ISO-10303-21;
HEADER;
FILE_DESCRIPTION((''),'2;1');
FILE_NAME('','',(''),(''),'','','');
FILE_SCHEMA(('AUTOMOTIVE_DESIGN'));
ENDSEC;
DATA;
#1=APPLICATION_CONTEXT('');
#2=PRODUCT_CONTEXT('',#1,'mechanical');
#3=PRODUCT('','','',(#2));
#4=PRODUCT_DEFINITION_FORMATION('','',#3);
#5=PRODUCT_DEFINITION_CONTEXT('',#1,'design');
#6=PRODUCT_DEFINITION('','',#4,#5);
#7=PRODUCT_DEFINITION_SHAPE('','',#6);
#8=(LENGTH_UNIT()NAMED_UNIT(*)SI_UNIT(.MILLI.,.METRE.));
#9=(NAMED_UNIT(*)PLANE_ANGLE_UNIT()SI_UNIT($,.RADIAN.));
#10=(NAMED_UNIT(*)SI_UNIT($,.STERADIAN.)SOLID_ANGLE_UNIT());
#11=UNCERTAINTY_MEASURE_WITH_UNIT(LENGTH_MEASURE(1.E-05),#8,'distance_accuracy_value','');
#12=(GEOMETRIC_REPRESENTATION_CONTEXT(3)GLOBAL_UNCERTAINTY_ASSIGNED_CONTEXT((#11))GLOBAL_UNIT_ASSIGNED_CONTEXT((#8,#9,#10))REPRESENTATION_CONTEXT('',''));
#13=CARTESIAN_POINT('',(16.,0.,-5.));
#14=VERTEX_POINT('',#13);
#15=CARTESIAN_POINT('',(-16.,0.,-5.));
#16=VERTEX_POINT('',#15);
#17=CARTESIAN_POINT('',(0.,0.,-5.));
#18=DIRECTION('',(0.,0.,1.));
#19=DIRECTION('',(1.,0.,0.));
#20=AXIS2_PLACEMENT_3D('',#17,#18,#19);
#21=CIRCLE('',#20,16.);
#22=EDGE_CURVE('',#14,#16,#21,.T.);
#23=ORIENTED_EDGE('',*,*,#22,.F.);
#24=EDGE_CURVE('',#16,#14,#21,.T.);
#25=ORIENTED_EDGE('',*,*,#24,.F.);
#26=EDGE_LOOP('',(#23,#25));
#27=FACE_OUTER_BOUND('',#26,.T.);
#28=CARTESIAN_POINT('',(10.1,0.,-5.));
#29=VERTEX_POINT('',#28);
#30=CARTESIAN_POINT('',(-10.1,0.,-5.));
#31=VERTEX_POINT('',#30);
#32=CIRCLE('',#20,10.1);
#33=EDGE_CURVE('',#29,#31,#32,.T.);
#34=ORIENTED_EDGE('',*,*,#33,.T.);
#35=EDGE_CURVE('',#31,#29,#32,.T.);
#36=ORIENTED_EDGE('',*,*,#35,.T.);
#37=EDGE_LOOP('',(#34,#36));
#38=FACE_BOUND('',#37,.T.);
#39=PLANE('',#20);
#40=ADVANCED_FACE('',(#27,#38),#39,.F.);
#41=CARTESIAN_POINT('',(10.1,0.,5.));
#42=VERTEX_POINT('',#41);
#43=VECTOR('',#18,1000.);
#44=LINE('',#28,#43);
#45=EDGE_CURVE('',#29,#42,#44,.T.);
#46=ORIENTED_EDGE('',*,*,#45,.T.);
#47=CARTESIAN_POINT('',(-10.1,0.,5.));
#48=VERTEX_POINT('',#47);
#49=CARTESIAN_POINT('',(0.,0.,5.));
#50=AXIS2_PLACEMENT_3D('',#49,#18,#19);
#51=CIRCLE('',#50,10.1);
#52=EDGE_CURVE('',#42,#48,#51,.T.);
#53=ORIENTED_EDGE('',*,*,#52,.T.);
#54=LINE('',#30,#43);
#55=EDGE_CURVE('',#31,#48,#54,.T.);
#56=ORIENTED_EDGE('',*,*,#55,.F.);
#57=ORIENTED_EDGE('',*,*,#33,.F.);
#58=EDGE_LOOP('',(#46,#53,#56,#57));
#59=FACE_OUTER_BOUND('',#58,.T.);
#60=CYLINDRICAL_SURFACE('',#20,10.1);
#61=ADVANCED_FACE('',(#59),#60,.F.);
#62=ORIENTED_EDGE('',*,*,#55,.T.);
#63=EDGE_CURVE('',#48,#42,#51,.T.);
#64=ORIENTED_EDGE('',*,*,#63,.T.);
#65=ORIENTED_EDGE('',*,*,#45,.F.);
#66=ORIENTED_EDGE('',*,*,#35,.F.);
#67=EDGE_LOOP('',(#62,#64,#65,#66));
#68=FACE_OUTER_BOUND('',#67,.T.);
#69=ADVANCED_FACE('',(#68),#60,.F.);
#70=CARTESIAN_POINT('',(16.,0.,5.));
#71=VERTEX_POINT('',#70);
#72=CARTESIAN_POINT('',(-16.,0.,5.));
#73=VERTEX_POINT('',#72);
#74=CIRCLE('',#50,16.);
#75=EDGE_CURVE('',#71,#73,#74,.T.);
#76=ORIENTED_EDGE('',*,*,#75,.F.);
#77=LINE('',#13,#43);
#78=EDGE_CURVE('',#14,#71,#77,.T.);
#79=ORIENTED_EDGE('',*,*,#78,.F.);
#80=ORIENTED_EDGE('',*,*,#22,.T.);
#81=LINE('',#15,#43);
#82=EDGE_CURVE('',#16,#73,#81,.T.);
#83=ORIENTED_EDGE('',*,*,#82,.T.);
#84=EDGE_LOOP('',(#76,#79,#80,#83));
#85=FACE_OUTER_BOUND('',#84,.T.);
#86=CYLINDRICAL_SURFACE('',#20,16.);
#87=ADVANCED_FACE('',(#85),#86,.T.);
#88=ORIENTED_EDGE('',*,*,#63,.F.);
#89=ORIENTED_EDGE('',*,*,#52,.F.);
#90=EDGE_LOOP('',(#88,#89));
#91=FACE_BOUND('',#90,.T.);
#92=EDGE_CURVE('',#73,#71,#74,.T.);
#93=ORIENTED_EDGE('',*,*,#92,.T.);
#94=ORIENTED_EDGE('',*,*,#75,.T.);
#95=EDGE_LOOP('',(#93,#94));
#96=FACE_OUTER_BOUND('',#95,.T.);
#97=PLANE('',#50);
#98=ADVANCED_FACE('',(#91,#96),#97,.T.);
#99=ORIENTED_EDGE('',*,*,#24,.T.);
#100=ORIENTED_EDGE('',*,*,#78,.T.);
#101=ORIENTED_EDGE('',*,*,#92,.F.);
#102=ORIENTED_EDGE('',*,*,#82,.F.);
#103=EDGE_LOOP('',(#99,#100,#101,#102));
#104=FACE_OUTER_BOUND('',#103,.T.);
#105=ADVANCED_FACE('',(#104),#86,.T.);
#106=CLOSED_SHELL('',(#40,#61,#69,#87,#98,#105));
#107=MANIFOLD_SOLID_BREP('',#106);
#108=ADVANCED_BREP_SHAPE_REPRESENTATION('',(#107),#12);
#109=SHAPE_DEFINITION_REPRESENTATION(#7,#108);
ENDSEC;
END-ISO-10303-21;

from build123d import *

# Parameters (mm, degrees)
SKETCH_1_R      = 16
SKETCH_1_R_2    = 10.1
EXTRUDE_1_DEPTH = 5


with BuildPart() as part:
    # 草图1 → 凸台-拉伸1 (new, symmetric)
    with BuildSketch(Plane.XY):
        Circle(SKETCH_1_R)
        Circle(SKETCH_1_R_2, mode=Mode.SUBTRACT)
    extrude(amount=EXTRUDE_1_DEPTH, both=True)


solid = part.part
